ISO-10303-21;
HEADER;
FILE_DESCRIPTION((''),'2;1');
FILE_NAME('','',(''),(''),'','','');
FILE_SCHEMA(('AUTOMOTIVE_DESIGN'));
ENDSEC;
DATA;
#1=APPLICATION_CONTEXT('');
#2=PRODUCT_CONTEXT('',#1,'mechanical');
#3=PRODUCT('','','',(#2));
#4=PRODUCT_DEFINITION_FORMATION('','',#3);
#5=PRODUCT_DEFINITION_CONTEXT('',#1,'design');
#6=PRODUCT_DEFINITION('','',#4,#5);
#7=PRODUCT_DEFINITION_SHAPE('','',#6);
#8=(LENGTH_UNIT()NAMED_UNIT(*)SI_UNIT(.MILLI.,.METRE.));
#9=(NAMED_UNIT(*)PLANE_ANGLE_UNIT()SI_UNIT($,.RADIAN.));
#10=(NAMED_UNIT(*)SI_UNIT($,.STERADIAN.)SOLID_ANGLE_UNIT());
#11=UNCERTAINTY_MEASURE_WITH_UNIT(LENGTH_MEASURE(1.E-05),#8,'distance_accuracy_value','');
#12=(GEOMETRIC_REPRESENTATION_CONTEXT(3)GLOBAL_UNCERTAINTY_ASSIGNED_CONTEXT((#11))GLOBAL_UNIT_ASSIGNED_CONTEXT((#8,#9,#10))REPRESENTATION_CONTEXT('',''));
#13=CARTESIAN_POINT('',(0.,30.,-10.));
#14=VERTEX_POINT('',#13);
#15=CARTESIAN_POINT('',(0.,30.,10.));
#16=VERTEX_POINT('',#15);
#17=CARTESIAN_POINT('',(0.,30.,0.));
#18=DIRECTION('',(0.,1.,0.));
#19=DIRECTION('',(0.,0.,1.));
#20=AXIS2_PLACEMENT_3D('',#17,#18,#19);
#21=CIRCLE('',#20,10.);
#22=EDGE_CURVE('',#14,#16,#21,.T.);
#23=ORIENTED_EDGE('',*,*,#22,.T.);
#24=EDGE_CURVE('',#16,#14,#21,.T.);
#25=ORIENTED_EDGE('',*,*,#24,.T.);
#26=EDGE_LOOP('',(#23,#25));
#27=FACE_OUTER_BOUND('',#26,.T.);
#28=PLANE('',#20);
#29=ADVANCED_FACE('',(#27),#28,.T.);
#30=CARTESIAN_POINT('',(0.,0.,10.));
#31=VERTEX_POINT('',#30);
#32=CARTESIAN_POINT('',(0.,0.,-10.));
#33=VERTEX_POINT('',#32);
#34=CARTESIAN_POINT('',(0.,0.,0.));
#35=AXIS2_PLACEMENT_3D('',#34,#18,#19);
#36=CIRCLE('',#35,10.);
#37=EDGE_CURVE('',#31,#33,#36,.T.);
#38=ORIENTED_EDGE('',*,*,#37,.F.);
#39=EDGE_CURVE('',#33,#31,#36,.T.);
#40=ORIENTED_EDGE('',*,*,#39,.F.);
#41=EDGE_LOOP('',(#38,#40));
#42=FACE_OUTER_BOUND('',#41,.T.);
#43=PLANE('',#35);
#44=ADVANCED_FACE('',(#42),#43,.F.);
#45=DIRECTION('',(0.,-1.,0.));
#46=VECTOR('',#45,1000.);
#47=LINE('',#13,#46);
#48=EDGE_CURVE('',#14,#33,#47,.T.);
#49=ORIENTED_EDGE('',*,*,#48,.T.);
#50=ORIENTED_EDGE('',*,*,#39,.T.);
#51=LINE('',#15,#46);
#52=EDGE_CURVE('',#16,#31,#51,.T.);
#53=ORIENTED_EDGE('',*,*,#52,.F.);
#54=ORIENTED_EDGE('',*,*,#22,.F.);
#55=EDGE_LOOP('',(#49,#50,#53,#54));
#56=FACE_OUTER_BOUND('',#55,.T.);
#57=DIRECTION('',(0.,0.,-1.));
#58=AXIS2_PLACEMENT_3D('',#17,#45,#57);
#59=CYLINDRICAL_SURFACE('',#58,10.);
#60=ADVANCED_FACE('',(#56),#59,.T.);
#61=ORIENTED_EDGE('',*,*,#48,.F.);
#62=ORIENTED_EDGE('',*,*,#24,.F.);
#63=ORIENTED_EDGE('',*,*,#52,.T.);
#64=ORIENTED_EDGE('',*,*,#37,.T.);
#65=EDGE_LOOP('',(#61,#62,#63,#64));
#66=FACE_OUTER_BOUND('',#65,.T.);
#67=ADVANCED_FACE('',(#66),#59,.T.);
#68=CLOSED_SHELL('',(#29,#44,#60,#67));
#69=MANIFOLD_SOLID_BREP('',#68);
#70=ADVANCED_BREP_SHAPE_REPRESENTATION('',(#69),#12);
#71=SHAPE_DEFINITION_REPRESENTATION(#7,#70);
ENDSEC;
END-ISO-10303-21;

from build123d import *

# Parameters (mm, degrees)
SKETCH1_R           = 10
BOSS_EXTRUDE1_DEPTH = 30


with BuildPart() as part:
    # Sketch1 → Boss-Extrude1 (new body)
    with BuildSketch(Plane(origin=(0, 0, 0), x_dir=(1, 0, 0), z_dir=(0, 1, 0))):
        with Locations(Location((0, 0, 0), (0, 0, 270))):
            Circle(SKETCH1_R)
    extrude(amount=BOSS_EXTRUDE1_DEPTH)


solid = part.part
